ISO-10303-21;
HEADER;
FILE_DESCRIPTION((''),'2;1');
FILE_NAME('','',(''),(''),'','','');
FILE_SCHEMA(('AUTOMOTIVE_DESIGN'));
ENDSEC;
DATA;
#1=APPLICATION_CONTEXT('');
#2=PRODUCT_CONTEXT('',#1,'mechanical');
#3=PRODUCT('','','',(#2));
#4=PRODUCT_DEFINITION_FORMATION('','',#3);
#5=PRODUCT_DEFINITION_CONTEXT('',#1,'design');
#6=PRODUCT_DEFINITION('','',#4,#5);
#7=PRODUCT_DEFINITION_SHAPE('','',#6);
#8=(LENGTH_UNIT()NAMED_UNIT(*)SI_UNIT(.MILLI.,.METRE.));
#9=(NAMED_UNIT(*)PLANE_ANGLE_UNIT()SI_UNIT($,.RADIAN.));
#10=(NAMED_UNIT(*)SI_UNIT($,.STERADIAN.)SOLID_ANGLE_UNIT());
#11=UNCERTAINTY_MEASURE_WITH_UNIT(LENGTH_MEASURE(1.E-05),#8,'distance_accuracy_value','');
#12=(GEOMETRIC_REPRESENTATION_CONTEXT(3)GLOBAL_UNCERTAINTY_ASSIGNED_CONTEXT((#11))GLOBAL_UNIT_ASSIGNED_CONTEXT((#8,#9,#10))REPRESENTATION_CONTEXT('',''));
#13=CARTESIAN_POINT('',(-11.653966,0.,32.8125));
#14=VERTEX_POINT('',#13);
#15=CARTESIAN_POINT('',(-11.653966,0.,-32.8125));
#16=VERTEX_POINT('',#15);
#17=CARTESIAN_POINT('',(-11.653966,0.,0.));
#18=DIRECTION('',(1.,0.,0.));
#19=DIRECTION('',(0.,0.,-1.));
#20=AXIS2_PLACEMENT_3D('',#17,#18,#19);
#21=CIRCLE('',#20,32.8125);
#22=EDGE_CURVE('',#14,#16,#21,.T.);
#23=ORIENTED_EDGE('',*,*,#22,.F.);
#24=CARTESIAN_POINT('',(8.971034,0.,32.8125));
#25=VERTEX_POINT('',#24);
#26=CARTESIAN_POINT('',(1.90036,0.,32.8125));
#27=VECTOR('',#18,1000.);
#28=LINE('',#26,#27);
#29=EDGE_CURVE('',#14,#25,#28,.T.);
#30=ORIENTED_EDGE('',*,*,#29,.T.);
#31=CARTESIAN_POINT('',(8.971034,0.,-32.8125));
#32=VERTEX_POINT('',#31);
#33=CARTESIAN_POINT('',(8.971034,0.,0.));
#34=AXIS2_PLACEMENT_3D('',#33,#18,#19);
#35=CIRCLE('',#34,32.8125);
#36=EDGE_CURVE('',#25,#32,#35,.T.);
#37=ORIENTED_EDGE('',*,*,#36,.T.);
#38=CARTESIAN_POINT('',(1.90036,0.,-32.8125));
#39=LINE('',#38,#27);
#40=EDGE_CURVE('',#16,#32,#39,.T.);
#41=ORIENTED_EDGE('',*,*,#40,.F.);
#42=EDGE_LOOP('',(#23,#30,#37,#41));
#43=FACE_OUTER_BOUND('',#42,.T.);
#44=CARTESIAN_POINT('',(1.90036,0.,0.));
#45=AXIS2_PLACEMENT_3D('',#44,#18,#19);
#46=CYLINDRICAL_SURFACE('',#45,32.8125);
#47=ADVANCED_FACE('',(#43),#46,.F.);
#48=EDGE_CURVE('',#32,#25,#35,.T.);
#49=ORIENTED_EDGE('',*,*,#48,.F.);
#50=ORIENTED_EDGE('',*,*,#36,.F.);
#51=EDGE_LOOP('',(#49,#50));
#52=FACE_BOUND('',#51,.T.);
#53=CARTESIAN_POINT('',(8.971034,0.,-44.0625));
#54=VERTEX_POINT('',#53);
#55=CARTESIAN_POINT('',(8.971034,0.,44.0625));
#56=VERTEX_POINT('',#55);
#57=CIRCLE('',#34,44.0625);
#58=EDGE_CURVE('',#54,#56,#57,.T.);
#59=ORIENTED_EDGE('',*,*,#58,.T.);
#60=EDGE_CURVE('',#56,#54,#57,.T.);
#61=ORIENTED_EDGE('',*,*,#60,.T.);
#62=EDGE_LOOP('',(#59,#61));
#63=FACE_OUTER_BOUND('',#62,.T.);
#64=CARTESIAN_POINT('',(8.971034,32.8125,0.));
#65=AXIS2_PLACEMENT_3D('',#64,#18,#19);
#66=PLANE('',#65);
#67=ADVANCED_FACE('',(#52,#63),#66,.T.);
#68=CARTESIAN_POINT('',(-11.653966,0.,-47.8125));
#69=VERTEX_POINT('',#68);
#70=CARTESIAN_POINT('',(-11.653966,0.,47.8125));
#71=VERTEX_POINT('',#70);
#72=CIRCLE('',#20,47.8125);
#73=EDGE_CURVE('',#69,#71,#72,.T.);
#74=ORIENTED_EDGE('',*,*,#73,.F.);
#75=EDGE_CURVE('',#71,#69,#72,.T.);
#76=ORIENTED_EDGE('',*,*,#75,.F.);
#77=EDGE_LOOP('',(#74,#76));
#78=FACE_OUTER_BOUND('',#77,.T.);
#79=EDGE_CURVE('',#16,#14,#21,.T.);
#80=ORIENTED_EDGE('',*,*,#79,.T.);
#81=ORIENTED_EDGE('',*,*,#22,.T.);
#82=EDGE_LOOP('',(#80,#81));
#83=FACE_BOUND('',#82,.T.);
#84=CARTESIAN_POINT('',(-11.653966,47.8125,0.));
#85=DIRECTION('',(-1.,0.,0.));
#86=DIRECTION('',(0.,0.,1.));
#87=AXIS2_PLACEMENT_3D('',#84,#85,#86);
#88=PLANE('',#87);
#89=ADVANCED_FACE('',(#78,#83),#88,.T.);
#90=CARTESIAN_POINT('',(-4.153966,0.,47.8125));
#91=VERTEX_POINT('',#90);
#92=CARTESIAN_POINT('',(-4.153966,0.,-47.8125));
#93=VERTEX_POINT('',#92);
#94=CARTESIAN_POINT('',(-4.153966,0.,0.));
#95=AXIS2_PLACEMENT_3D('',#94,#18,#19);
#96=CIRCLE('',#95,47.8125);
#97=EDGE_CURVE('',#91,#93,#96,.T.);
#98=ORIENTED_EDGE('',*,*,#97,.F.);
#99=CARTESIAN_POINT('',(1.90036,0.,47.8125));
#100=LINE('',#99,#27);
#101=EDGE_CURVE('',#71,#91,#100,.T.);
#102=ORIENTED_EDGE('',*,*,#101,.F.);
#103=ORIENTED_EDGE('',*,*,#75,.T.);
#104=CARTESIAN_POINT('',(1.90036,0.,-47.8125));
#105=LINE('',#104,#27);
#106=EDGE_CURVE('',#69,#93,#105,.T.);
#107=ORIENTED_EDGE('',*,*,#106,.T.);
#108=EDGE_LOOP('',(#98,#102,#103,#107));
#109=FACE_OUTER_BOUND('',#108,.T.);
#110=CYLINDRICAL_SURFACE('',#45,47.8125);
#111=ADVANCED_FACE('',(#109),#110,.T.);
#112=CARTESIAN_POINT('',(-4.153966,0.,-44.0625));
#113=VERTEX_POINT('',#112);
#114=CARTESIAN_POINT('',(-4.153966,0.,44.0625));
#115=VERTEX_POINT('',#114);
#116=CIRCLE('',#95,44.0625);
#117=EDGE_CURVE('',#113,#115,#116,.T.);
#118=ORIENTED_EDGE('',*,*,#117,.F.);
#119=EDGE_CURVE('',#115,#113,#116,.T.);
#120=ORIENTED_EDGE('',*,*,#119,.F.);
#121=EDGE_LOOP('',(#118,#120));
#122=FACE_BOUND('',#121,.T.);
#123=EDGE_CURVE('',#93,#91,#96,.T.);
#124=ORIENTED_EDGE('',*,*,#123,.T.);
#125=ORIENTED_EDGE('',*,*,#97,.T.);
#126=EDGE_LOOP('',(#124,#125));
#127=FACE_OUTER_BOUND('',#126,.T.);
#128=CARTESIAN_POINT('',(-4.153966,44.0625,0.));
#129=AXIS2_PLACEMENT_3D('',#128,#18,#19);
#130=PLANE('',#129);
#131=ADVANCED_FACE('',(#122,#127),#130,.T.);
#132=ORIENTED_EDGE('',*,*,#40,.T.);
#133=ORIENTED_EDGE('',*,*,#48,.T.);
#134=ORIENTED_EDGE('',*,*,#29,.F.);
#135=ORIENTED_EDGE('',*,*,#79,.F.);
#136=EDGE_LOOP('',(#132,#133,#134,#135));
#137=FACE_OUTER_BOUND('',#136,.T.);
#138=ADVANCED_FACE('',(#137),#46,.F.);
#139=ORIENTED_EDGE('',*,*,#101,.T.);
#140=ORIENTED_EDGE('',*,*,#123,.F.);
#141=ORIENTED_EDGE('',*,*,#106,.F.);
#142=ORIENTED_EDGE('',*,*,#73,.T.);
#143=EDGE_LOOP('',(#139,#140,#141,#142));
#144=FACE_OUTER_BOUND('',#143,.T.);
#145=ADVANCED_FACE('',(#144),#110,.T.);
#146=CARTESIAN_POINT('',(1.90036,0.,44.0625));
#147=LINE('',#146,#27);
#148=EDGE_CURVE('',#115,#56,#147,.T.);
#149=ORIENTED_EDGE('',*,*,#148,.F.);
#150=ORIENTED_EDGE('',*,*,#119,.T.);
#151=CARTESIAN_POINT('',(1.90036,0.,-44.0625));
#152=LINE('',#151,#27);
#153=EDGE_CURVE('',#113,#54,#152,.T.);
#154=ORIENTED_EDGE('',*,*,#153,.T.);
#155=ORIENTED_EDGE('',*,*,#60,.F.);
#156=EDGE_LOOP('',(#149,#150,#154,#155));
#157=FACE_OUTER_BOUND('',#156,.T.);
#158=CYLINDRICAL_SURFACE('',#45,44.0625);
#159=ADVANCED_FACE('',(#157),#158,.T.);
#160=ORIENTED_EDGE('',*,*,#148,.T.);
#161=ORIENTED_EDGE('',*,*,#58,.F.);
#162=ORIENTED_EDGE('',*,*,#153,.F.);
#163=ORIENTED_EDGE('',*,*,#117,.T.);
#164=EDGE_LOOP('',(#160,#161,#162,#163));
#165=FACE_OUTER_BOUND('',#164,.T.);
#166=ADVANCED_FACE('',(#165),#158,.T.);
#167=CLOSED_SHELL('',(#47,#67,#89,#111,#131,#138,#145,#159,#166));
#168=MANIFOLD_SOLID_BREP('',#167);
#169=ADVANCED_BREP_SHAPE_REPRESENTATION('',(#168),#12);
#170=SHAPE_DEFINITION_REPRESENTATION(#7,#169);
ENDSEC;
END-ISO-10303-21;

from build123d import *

# Parameters (mm, degrees)
SCALE_1_SCALE = 1.875


with BuildPart() as part:
    # Sketch1 → Revolve1 (revolve)
    with BuildSketch(Plane.XY, mode=Mode.PRIVATE) as revolve1_sk:
        Polygon((-7.228973684, 17.5), (3.771026316, 17.5), (3.771026316, 23.5), (-3.228973684, 23.5), (-3.228973684, 25.5), (-7.228973684, 25.5), align=None)
    revolve(revolve1_sk.sketch.rotate(Axis((0, 0, 0), (-1, 0, 0)), 90), axis=Axis((0, 0, 0), (-1, 0, 0)))


with BuildPart() as part_1:
    # Scale 1: scaled about (-2.17184005, 0, 0)
    add(part.part.scale(SCALE_1_SCALE).moved(Location((1.900360044, 0, 0))))


solid = part_1.part
